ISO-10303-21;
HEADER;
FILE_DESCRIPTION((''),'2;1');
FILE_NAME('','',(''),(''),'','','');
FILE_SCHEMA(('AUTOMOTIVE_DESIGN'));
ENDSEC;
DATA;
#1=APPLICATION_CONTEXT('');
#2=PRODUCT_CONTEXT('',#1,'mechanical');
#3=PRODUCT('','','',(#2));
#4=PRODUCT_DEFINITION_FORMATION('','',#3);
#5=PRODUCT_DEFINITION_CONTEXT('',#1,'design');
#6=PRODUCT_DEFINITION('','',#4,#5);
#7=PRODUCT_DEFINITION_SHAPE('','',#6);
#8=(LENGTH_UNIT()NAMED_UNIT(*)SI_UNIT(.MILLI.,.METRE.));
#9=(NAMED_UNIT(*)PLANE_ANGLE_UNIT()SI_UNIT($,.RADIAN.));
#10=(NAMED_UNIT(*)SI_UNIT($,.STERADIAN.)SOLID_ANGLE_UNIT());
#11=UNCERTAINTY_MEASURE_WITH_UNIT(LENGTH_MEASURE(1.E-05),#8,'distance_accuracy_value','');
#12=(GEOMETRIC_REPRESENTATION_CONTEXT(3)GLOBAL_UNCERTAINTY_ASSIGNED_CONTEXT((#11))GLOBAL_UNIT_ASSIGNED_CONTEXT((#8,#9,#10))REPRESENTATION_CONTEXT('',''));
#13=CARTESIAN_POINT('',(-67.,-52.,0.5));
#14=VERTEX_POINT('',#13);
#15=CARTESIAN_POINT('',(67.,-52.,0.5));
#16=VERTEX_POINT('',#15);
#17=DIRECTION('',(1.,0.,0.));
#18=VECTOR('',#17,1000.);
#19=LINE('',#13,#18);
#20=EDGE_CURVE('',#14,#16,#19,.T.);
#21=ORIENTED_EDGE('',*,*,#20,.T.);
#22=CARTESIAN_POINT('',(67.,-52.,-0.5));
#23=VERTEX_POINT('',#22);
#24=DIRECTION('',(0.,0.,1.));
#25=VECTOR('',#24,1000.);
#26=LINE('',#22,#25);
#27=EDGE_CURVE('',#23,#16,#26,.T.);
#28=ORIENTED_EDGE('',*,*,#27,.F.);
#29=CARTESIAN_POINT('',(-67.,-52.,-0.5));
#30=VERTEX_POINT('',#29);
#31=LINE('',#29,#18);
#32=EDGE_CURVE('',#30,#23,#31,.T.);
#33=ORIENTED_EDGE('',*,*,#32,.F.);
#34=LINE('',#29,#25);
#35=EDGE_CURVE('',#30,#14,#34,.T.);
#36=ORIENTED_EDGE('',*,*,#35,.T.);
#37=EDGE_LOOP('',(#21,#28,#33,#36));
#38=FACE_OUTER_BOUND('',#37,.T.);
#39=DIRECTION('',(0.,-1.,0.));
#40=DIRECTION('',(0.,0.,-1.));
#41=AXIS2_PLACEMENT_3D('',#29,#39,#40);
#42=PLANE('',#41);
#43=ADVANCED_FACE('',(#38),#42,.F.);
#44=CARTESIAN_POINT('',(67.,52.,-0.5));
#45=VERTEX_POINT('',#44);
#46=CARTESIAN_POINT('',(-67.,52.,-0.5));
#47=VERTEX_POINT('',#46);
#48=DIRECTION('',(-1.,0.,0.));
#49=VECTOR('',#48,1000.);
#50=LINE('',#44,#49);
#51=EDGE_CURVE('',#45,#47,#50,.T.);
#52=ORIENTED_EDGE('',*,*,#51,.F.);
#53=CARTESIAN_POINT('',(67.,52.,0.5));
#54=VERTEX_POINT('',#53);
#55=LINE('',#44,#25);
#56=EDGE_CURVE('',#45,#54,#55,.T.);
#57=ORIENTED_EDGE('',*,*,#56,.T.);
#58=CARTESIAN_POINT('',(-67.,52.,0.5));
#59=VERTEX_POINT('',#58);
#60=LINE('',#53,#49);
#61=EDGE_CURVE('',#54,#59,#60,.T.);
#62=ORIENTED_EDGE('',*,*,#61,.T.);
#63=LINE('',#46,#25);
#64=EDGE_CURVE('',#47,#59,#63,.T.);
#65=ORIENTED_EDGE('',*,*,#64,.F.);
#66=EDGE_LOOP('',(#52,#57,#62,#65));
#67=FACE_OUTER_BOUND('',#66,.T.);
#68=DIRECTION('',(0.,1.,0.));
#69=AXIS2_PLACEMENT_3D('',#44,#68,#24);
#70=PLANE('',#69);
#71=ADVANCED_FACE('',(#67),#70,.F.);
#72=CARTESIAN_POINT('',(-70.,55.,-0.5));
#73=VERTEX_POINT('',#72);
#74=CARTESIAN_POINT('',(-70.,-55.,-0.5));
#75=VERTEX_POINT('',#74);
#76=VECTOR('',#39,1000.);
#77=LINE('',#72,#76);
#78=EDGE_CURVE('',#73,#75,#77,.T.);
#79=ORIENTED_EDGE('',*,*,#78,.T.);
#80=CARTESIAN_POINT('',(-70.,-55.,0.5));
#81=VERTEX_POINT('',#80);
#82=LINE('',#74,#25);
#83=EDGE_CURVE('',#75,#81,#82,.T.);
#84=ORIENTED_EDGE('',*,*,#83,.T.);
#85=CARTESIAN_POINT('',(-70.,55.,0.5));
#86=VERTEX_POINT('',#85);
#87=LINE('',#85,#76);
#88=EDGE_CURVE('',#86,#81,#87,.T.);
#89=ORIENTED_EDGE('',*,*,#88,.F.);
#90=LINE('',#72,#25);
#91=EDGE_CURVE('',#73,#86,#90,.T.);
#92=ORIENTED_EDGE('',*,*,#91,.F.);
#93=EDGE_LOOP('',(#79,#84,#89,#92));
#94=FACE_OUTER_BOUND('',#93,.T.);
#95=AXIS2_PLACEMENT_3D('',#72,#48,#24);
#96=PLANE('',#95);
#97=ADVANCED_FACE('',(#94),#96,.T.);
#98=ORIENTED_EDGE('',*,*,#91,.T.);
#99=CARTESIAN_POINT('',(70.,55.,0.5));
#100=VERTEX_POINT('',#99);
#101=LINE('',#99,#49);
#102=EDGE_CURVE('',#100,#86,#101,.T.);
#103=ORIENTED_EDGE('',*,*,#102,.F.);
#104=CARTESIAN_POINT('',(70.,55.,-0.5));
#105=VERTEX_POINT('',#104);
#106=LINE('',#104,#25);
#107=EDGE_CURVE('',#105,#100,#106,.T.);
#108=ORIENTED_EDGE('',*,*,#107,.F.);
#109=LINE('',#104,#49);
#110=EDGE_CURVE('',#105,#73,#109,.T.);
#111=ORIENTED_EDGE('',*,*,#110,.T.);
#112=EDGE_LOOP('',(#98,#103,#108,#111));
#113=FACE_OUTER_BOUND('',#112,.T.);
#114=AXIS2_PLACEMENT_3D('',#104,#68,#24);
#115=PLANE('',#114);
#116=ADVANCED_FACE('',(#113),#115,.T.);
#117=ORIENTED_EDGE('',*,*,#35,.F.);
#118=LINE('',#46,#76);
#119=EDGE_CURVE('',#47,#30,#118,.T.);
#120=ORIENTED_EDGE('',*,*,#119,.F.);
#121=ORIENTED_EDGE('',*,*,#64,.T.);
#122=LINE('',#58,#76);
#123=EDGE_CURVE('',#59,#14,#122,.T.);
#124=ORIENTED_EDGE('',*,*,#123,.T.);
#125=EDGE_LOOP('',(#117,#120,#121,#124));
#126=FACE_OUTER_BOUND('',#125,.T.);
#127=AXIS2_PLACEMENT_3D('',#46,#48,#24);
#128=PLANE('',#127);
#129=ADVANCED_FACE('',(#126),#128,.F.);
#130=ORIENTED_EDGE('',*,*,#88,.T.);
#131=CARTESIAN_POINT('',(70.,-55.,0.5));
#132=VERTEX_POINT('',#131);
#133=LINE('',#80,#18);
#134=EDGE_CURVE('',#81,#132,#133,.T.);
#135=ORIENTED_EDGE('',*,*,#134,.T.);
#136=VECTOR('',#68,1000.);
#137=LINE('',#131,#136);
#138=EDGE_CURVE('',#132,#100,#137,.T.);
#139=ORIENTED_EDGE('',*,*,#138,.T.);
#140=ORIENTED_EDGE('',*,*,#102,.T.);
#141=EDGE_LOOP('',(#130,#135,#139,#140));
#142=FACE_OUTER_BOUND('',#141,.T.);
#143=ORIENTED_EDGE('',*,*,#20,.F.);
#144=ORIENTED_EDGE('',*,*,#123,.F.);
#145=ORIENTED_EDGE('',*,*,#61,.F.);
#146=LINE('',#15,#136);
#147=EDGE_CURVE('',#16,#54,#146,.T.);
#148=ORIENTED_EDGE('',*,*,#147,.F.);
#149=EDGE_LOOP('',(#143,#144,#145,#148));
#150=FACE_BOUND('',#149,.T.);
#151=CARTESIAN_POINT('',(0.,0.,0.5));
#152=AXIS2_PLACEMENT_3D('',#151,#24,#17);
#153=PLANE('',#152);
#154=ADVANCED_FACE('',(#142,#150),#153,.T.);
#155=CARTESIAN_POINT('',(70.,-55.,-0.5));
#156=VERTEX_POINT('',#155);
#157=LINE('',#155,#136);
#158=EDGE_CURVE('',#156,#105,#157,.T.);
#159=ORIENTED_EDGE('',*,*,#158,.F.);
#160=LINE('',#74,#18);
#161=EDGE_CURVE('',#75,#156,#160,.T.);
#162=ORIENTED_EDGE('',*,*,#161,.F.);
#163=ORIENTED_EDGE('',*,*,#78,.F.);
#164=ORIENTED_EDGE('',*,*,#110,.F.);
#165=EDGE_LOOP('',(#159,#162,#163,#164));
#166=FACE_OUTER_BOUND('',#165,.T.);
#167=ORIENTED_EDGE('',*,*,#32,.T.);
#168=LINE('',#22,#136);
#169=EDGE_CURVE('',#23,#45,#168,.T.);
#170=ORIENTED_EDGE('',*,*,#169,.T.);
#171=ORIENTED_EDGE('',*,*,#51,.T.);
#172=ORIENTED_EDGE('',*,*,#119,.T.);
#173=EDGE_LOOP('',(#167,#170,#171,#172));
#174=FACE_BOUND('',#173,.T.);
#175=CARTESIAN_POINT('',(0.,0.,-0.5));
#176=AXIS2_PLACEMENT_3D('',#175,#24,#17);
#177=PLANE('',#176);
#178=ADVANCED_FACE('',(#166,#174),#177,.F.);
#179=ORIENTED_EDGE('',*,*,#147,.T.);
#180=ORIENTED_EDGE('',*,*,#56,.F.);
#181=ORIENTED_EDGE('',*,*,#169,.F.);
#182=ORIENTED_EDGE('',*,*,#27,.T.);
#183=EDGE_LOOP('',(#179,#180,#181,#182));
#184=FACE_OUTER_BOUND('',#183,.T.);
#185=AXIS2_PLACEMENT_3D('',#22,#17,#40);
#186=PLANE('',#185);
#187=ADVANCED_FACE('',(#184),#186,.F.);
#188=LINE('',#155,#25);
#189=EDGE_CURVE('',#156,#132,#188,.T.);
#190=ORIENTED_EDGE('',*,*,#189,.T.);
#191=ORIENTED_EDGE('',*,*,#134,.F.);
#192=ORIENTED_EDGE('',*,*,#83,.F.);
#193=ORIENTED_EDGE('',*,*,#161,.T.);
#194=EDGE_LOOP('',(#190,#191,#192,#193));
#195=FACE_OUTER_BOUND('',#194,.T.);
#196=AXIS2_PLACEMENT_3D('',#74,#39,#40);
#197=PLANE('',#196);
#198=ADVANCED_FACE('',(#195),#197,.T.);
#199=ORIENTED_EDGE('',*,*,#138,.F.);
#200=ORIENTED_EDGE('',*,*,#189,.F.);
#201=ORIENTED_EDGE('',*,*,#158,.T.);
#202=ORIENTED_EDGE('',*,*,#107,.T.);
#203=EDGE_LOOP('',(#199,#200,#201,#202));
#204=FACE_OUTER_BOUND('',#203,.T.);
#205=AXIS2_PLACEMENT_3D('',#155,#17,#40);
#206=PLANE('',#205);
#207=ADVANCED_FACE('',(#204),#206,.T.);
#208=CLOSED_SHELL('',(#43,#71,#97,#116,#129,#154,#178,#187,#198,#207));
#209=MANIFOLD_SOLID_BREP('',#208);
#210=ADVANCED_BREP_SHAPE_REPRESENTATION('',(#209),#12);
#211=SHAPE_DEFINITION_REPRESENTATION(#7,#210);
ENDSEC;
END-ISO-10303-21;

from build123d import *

# Parameters (mm, degrees)
SKETCH_1_W      = 140
SKETCH_1_H      = 110
SKETCH_1_W_2    = 134
SKETCH_1_H_2    = 104
EXTRUDE_1_DEPTH = 0.5


with BuildPart() as part:
    # 草图1 → 凸台-拉伸1 (new, symmetric)
    with BuildSketch(Plane.XY):
        Rectangle(SKETCH_1_W, SKETCH_1_H)
        Rectangle(SKETCH_1_W_2, SKETCH_1_H_2, mode=Mode.SUBTRACT)
    extrude(amount=EXTRUDE_1_DEPTH, both=True)


solid = part.part
